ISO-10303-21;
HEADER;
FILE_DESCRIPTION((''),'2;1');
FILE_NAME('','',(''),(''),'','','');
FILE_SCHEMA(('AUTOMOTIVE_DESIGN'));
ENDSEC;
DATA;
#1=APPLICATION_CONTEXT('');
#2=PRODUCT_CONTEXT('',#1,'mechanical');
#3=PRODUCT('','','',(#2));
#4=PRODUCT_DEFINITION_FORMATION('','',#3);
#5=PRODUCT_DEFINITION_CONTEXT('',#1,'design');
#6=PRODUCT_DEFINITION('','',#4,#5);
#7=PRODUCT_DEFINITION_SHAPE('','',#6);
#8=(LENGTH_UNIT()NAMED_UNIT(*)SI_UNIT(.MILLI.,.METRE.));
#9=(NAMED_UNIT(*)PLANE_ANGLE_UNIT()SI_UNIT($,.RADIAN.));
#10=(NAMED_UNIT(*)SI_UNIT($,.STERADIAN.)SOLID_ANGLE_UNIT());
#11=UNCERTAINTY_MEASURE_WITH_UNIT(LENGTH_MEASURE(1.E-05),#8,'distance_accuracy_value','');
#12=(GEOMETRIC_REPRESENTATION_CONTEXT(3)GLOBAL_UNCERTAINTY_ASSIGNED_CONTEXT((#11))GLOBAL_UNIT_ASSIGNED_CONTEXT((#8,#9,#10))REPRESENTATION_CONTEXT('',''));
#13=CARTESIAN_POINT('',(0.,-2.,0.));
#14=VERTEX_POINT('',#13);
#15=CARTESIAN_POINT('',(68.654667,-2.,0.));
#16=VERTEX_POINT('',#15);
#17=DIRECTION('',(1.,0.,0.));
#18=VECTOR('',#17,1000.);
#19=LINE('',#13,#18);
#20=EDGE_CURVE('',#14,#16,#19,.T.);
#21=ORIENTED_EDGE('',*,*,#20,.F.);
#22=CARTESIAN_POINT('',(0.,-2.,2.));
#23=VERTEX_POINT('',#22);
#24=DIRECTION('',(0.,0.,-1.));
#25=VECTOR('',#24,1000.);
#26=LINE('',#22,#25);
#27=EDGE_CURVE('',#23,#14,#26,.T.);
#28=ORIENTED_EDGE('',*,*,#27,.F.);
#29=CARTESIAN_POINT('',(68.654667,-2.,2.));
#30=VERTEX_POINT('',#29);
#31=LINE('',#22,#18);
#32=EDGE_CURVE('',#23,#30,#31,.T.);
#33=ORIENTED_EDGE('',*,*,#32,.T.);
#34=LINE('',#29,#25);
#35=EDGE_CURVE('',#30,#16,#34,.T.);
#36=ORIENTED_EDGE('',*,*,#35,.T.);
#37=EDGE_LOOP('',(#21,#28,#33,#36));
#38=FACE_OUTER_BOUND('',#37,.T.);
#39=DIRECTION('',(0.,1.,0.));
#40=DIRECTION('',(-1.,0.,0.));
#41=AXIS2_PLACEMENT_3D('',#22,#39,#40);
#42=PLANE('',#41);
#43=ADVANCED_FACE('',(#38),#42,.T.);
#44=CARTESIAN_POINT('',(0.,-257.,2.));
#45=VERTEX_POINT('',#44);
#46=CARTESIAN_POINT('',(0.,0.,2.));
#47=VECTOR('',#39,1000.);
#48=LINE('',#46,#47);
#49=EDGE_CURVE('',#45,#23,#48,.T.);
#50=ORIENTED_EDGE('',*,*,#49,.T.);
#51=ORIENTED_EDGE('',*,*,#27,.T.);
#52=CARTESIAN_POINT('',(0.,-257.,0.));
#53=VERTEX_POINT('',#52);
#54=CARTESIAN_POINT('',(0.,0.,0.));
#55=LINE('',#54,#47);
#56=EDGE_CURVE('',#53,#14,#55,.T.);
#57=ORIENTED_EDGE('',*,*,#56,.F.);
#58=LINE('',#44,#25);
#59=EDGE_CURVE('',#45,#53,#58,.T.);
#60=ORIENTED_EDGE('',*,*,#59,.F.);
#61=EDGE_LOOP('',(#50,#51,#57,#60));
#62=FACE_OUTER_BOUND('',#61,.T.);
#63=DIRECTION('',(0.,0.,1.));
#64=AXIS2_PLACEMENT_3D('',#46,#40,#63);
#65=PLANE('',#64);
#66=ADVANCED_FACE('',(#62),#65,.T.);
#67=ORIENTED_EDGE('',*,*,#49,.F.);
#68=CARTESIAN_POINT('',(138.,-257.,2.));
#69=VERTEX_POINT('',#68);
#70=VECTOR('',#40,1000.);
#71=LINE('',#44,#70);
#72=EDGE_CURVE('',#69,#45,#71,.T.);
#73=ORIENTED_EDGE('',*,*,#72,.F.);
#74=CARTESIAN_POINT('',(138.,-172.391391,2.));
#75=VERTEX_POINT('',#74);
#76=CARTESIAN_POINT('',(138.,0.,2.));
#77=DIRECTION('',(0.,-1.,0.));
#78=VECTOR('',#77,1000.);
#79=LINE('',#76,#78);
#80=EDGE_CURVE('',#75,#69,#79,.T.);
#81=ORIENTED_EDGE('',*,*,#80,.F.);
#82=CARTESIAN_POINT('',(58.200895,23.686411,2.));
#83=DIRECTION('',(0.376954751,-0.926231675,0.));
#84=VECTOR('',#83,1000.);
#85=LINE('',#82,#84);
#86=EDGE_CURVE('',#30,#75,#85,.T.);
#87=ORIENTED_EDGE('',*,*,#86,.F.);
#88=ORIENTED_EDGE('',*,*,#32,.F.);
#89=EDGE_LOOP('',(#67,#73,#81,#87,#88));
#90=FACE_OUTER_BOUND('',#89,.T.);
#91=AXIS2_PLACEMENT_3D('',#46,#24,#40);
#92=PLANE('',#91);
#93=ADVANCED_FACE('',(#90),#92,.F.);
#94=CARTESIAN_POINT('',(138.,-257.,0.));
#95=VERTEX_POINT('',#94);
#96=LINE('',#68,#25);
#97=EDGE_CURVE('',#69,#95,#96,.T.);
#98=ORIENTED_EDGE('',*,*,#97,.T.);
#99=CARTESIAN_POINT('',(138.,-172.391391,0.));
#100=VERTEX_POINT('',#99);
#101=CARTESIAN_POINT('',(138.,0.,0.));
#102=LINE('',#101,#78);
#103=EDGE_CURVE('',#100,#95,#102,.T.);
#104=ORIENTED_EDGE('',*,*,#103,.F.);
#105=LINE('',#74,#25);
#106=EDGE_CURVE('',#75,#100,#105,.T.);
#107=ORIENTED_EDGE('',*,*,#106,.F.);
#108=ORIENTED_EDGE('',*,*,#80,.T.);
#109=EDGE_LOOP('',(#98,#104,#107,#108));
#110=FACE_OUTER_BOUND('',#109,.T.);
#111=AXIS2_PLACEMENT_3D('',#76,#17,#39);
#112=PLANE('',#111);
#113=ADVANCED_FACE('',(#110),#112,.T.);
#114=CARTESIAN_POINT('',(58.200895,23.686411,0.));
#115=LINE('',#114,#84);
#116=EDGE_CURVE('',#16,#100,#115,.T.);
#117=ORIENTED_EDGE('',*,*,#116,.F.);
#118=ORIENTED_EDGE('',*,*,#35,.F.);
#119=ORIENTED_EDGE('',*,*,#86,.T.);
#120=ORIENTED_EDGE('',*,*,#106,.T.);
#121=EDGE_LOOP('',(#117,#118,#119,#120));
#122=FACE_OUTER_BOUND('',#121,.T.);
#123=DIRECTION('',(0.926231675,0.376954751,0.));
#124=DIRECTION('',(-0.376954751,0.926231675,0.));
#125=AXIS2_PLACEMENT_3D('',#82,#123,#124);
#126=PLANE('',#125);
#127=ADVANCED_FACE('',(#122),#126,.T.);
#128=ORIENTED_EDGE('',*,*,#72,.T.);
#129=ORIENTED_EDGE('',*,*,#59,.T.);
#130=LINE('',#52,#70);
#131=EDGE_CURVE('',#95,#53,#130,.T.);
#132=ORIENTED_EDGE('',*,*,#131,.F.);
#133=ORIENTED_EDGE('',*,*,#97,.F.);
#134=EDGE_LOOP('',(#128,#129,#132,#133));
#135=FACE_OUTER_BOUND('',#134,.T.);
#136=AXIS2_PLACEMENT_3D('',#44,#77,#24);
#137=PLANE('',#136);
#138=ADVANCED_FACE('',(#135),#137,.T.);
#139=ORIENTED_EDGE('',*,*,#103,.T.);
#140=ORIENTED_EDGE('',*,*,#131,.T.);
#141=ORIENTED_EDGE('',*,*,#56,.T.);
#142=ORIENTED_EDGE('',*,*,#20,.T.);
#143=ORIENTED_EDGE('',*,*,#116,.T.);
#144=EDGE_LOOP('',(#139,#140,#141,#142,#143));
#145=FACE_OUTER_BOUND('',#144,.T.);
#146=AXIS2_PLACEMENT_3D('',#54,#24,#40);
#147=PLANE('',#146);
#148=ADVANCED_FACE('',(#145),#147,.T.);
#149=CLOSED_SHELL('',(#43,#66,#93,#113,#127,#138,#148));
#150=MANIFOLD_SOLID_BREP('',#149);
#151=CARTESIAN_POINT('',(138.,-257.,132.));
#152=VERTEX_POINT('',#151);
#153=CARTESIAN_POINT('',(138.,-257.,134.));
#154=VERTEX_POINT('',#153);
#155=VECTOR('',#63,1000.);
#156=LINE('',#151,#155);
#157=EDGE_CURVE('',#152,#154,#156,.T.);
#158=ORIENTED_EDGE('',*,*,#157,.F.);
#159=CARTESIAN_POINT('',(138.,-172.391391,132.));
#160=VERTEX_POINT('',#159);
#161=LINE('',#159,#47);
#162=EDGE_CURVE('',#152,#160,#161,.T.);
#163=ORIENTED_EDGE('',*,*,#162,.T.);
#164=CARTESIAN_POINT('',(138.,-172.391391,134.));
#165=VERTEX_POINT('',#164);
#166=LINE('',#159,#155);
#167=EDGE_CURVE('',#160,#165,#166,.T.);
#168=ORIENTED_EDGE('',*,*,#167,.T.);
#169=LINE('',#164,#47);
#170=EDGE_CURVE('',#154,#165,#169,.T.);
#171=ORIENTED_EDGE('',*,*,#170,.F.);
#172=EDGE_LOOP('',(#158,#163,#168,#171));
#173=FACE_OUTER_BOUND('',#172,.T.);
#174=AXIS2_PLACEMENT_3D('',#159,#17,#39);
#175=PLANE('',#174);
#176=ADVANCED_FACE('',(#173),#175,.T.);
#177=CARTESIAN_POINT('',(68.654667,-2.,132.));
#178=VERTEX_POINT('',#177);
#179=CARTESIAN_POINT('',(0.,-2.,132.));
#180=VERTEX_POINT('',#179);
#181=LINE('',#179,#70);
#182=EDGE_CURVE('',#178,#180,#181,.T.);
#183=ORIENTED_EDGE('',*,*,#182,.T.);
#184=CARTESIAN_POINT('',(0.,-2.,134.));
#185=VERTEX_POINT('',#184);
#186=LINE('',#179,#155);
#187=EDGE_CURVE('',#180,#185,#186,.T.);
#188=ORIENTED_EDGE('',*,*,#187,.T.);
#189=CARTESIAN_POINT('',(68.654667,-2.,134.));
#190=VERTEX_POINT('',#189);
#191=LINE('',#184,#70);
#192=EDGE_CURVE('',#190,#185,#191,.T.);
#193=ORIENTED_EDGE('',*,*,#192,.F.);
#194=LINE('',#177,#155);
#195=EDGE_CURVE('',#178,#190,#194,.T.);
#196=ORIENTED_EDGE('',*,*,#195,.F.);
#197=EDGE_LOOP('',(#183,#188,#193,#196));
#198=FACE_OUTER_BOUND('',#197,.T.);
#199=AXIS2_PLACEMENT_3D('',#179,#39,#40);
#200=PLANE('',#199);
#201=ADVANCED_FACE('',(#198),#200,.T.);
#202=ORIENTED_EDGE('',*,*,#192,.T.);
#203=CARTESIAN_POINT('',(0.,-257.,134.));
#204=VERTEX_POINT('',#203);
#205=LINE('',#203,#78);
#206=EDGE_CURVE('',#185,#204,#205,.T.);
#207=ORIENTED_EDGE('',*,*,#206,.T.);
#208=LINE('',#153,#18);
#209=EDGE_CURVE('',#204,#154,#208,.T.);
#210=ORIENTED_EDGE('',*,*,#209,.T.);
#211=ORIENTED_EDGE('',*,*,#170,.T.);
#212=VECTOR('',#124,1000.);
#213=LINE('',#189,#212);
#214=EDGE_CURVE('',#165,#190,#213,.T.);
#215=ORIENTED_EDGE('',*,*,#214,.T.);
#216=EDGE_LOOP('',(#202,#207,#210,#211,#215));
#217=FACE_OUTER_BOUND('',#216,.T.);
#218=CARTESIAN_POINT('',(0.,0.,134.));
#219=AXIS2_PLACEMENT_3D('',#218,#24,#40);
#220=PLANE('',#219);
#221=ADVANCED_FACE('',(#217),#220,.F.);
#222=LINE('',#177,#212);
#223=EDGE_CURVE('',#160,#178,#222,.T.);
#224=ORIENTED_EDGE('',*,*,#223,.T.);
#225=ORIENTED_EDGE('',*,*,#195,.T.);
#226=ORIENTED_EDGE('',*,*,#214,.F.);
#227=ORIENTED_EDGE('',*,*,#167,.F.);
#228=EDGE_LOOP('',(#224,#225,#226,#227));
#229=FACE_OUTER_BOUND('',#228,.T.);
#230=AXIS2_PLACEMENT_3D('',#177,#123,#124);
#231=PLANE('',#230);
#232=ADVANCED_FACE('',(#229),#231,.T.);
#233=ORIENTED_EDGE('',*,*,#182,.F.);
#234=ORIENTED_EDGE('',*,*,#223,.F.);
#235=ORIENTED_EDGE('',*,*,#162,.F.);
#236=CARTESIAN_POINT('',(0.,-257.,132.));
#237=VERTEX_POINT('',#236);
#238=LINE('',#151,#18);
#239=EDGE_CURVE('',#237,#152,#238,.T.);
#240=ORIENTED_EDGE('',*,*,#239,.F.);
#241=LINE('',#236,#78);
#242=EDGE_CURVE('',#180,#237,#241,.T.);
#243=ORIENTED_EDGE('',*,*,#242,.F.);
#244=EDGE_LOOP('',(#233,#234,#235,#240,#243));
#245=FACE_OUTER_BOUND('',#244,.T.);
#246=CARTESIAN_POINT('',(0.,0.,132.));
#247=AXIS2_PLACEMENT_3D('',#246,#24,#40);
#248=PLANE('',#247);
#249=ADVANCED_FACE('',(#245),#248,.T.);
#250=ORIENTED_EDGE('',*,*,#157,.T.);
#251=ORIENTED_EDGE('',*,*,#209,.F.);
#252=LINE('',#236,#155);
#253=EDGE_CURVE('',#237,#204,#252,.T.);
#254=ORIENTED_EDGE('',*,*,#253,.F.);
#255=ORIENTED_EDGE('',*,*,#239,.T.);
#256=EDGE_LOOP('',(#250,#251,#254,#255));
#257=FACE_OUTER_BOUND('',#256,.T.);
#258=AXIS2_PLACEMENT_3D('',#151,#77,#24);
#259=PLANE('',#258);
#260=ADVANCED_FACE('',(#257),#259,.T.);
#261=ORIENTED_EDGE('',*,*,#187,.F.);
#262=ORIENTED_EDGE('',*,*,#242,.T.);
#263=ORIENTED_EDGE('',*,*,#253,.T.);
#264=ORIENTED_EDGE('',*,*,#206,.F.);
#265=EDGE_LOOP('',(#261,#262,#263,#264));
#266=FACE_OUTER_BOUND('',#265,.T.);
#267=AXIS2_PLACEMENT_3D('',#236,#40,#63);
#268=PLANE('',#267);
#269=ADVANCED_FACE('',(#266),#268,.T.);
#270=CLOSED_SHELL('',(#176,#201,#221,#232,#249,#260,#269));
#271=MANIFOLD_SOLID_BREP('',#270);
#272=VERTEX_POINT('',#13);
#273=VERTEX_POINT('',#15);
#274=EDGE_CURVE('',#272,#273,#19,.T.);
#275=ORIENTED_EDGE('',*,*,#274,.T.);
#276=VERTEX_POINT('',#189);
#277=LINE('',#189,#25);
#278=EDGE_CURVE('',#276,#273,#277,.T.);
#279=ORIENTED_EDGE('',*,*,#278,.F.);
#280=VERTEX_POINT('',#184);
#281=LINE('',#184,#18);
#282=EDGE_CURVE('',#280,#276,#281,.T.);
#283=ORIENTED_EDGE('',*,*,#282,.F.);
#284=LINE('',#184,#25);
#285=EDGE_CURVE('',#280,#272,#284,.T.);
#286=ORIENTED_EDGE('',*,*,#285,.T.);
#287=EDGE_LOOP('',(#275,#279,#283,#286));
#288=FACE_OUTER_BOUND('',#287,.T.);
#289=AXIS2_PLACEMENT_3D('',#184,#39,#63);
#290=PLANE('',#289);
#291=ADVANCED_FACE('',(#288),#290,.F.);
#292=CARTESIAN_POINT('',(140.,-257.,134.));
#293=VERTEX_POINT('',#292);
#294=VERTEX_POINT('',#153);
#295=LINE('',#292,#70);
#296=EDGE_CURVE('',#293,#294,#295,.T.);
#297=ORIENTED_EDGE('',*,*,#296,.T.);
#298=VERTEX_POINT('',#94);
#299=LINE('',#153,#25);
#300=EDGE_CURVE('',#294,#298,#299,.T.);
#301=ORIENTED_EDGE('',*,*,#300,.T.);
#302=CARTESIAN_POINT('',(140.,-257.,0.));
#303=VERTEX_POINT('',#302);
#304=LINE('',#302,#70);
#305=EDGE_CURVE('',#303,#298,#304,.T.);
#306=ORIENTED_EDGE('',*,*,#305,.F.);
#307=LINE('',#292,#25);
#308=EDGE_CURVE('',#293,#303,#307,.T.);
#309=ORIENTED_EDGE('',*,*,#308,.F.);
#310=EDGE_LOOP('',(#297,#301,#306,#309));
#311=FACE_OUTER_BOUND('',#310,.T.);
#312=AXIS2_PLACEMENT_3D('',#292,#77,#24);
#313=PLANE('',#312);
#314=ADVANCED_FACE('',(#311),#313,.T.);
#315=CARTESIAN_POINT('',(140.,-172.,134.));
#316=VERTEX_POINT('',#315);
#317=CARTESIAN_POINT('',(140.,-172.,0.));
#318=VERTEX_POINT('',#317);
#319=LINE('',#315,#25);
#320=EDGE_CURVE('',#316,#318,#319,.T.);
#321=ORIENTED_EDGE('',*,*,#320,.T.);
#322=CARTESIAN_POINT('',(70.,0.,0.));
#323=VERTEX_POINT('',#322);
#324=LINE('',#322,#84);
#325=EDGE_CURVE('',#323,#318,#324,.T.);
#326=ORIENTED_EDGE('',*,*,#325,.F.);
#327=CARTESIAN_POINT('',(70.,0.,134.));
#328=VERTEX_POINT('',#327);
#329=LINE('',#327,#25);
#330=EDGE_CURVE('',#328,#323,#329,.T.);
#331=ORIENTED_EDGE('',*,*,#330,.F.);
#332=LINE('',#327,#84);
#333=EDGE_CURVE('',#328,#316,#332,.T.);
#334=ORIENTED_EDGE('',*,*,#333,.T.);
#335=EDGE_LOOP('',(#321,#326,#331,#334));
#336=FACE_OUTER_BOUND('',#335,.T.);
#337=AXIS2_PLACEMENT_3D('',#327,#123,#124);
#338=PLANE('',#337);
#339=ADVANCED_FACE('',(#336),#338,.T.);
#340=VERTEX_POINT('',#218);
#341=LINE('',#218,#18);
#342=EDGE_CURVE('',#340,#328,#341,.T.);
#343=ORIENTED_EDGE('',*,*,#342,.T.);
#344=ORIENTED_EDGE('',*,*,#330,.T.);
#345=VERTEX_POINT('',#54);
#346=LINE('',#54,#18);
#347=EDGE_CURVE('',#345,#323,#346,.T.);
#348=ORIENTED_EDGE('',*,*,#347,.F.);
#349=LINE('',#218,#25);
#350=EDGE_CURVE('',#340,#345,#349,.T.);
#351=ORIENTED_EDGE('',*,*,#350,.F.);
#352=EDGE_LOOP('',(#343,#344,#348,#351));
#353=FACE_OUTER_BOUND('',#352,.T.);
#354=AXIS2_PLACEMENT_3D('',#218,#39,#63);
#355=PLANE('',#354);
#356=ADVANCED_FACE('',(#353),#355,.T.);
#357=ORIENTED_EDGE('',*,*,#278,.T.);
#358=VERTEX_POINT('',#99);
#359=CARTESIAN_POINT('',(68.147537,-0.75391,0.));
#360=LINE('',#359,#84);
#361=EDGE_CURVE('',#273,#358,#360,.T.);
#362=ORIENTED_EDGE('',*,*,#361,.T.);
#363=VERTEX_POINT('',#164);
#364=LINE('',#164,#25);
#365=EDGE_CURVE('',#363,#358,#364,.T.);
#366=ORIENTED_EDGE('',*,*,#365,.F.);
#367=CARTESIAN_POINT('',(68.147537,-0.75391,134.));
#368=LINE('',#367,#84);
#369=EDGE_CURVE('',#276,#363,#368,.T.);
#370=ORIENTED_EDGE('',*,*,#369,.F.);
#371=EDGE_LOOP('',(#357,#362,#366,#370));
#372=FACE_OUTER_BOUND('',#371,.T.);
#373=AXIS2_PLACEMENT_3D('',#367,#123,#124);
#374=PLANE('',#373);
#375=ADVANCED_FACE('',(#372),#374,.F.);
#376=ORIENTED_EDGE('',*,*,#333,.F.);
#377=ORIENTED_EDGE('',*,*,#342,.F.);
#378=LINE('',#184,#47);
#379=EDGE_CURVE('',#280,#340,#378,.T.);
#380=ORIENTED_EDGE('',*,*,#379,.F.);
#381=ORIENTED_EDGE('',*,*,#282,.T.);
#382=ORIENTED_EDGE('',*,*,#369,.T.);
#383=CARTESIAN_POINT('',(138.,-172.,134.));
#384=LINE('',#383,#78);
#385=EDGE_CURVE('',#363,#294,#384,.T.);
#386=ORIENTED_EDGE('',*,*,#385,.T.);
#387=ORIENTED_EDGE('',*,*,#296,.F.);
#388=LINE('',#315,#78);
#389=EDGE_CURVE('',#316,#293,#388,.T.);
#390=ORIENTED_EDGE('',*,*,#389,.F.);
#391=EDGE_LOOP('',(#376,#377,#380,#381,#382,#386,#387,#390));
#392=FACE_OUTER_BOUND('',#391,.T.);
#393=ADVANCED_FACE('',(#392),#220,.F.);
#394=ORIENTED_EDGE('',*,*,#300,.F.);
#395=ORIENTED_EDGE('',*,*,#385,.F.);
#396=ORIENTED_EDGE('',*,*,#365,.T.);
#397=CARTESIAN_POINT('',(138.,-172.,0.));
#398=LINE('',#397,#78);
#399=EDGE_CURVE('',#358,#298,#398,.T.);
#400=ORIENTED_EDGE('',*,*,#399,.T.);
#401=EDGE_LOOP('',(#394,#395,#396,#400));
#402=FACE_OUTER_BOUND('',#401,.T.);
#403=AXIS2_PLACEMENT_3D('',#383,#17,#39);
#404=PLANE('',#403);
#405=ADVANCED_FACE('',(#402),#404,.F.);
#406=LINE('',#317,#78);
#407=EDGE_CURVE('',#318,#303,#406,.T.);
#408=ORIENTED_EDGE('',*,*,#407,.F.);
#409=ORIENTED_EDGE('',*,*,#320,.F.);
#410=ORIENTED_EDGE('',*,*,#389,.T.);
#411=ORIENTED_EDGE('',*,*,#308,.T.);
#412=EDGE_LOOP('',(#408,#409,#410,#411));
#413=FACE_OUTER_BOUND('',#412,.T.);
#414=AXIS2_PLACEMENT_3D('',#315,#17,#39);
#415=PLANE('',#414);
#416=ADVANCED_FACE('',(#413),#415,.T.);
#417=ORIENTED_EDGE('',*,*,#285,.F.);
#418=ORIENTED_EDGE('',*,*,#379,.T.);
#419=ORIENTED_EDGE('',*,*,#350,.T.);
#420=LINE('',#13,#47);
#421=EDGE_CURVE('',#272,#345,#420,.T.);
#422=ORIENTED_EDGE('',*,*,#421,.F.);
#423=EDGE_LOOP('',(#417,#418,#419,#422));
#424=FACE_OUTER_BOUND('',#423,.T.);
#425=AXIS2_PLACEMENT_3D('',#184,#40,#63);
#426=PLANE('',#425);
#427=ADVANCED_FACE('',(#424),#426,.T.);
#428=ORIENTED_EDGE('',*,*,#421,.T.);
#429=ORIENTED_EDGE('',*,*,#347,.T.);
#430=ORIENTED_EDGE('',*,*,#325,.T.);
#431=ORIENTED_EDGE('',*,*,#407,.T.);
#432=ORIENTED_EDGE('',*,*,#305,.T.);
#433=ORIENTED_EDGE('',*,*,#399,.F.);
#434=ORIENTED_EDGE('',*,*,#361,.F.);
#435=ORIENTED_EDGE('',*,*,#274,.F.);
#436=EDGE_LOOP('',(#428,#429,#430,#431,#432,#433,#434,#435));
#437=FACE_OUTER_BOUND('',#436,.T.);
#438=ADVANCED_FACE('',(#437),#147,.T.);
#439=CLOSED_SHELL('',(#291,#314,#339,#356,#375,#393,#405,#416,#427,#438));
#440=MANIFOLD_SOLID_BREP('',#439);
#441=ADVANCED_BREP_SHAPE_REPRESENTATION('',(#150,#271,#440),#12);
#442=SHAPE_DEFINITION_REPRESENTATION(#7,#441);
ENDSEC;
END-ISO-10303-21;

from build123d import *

# Parameters (mm, degrees)
EXTRUDE_1_DEPTH   = 134
EXTRUDE_1_2_DEPTH = 2
EXTRUDE_START     = -134
EXTRUDE_2_DEPTH   = 2


with BuildPart() as part:
    # 草图1 → Extrude 1 (new body)
    with BuildSketch(Plane.XY):
        Polygon((0, 0), (70, 0), (140, -172), (140, -257), (138, -257), (138, -172.391390876), (68.654666504, -2), (0, -2), align=None)
    extrude(amount=EXTRUDE_1_DEPTH)


with BuildPart() as body_2:
    # 草图2 → Extrude 1 2 (new body)
    with BuildSketch(Plane.XY.offset(134)):
        Polygon((0, -2), (68.654666504, -2), (138, -172.391390876), (138, -257), (0, -257), align=None)
    extrude(amount=-EXTRUDE_1_2_DEPTH)


with BuildPart() as body_3:
    # 草图2<2> → 凸台-拉伸2 (new body)
    with BuildSketch(Plane.XY.offset(134).offset(EXTRUDE_START)):
        Polygon((0, -2), (68.654666504, -2), (138, -172.391390876), (138, -257), (0, -257), align=None)
    extrude(amount=EXTRUDE_2_DEPTH)


solid = Compound([part.part, body_2.part, body_3.part])
